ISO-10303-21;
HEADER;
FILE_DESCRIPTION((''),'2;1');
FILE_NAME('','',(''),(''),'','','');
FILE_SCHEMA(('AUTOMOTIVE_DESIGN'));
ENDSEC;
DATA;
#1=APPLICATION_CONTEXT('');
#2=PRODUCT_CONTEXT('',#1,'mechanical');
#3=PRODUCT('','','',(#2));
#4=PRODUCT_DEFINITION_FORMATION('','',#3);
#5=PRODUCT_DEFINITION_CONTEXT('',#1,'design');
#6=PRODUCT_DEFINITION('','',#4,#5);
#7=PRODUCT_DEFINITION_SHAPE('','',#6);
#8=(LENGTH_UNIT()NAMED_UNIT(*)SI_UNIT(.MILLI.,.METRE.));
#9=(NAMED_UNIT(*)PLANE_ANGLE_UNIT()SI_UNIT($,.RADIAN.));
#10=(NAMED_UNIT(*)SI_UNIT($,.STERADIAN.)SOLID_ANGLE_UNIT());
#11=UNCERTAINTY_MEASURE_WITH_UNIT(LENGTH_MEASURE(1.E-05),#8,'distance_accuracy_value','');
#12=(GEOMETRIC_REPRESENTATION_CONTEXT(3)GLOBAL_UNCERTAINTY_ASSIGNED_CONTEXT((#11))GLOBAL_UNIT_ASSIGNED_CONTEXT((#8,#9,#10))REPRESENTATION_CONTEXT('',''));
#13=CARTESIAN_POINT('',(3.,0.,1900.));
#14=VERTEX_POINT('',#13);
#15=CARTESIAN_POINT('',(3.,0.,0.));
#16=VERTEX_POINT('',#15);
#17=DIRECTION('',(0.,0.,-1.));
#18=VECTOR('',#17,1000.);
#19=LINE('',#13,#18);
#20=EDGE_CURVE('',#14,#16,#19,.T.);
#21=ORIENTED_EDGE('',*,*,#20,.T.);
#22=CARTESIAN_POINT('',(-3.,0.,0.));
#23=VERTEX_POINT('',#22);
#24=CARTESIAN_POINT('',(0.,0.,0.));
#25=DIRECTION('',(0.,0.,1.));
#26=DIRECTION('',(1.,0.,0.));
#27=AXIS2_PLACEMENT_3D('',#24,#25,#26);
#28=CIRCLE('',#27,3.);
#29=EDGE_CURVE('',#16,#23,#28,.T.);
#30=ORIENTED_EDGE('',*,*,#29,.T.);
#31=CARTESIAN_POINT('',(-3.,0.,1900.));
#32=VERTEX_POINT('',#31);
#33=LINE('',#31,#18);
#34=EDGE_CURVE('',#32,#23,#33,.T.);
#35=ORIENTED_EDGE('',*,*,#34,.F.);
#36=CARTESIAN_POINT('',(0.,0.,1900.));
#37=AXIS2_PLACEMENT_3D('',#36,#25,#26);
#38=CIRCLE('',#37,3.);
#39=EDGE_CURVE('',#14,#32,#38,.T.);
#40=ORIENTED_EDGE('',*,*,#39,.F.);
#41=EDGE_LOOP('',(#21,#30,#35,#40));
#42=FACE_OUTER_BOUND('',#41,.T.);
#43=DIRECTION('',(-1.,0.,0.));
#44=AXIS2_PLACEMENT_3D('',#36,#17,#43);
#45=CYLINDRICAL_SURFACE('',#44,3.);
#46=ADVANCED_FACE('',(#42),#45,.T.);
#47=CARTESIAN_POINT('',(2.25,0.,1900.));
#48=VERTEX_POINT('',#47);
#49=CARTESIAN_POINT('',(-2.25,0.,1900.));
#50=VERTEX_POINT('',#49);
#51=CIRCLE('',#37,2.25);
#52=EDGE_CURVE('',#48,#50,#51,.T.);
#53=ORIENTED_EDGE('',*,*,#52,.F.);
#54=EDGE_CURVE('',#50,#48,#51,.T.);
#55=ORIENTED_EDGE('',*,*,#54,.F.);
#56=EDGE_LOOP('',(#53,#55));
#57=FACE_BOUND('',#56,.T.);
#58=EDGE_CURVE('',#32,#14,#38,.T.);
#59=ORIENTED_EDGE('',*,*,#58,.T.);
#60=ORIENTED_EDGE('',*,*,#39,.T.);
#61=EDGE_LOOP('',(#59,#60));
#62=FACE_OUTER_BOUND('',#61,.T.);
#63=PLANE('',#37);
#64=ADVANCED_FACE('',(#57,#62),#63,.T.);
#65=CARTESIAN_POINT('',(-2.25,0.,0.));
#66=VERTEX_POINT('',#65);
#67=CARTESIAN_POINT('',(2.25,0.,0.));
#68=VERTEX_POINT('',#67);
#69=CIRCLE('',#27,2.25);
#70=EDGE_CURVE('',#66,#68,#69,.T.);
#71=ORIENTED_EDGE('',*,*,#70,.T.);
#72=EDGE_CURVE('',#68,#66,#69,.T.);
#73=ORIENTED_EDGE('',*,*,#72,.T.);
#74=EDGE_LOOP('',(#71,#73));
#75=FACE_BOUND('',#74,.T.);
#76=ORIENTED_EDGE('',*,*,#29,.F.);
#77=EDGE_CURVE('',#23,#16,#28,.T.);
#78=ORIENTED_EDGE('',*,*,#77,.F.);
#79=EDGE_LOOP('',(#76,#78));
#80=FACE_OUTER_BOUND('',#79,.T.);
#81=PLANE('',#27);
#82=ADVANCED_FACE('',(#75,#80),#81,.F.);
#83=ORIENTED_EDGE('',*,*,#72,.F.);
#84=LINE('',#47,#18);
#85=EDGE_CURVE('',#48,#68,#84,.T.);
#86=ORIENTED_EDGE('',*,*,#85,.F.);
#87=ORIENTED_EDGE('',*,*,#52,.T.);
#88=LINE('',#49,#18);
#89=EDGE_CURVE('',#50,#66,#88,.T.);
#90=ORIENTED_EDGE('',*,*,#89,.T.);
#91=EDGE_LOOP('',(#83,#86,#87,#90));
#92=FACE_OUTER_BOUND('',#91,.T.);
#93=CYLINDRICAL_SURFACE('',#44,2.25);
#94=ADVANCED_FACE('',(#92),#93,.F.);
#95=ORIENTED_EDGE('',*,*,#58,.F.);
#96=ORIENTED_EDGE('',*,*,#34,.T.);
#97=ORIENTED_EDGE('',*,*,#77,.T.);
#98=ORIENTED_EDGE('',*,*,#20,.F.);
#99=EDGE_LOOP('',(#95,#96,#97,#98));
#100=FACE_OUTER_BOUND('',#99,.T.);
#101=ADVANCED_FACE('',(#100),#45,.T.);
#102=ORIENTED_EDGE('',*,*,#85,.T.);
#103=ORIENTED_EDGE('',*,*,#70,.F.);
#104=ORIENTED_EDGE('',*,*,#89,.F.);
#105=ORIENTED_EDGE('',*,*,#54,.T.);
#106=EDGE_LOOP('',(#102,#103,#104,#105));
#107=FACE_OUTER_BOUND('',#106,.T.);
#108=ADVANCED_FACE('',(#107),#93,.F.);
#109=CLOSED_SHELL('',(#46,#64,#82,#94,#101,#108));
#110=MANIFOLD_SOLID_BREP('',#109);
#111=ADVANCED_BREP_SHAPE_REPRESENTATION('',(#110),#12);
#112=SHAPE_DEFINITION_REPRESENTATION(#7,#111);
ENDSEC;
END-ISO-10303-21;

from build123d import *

# Parameters (mm, degrees)
SKETCH1_R           = 3
SKETCH1_R_2         = 2.25
BOSS_EXTRUDE1_DEPTH = 1900


with BuildPart() as part:
    # Sketch1 → Boss-Extrude1 (new body)
    with BuildSketch(Plane.XY):
        with Locations(Location((0, 0, 0), (0, 0, 180))):
            Circle(SKETCH1_R)
        with Locations(Location((0, 0, 0), (0, 0, 180))):
            Circle(SKETCH1_R_2, mode=Mode.SUBTRACT)
    extrude(amount=BOSS_EXTRUDE1_DEPTH)


solid = part.part
